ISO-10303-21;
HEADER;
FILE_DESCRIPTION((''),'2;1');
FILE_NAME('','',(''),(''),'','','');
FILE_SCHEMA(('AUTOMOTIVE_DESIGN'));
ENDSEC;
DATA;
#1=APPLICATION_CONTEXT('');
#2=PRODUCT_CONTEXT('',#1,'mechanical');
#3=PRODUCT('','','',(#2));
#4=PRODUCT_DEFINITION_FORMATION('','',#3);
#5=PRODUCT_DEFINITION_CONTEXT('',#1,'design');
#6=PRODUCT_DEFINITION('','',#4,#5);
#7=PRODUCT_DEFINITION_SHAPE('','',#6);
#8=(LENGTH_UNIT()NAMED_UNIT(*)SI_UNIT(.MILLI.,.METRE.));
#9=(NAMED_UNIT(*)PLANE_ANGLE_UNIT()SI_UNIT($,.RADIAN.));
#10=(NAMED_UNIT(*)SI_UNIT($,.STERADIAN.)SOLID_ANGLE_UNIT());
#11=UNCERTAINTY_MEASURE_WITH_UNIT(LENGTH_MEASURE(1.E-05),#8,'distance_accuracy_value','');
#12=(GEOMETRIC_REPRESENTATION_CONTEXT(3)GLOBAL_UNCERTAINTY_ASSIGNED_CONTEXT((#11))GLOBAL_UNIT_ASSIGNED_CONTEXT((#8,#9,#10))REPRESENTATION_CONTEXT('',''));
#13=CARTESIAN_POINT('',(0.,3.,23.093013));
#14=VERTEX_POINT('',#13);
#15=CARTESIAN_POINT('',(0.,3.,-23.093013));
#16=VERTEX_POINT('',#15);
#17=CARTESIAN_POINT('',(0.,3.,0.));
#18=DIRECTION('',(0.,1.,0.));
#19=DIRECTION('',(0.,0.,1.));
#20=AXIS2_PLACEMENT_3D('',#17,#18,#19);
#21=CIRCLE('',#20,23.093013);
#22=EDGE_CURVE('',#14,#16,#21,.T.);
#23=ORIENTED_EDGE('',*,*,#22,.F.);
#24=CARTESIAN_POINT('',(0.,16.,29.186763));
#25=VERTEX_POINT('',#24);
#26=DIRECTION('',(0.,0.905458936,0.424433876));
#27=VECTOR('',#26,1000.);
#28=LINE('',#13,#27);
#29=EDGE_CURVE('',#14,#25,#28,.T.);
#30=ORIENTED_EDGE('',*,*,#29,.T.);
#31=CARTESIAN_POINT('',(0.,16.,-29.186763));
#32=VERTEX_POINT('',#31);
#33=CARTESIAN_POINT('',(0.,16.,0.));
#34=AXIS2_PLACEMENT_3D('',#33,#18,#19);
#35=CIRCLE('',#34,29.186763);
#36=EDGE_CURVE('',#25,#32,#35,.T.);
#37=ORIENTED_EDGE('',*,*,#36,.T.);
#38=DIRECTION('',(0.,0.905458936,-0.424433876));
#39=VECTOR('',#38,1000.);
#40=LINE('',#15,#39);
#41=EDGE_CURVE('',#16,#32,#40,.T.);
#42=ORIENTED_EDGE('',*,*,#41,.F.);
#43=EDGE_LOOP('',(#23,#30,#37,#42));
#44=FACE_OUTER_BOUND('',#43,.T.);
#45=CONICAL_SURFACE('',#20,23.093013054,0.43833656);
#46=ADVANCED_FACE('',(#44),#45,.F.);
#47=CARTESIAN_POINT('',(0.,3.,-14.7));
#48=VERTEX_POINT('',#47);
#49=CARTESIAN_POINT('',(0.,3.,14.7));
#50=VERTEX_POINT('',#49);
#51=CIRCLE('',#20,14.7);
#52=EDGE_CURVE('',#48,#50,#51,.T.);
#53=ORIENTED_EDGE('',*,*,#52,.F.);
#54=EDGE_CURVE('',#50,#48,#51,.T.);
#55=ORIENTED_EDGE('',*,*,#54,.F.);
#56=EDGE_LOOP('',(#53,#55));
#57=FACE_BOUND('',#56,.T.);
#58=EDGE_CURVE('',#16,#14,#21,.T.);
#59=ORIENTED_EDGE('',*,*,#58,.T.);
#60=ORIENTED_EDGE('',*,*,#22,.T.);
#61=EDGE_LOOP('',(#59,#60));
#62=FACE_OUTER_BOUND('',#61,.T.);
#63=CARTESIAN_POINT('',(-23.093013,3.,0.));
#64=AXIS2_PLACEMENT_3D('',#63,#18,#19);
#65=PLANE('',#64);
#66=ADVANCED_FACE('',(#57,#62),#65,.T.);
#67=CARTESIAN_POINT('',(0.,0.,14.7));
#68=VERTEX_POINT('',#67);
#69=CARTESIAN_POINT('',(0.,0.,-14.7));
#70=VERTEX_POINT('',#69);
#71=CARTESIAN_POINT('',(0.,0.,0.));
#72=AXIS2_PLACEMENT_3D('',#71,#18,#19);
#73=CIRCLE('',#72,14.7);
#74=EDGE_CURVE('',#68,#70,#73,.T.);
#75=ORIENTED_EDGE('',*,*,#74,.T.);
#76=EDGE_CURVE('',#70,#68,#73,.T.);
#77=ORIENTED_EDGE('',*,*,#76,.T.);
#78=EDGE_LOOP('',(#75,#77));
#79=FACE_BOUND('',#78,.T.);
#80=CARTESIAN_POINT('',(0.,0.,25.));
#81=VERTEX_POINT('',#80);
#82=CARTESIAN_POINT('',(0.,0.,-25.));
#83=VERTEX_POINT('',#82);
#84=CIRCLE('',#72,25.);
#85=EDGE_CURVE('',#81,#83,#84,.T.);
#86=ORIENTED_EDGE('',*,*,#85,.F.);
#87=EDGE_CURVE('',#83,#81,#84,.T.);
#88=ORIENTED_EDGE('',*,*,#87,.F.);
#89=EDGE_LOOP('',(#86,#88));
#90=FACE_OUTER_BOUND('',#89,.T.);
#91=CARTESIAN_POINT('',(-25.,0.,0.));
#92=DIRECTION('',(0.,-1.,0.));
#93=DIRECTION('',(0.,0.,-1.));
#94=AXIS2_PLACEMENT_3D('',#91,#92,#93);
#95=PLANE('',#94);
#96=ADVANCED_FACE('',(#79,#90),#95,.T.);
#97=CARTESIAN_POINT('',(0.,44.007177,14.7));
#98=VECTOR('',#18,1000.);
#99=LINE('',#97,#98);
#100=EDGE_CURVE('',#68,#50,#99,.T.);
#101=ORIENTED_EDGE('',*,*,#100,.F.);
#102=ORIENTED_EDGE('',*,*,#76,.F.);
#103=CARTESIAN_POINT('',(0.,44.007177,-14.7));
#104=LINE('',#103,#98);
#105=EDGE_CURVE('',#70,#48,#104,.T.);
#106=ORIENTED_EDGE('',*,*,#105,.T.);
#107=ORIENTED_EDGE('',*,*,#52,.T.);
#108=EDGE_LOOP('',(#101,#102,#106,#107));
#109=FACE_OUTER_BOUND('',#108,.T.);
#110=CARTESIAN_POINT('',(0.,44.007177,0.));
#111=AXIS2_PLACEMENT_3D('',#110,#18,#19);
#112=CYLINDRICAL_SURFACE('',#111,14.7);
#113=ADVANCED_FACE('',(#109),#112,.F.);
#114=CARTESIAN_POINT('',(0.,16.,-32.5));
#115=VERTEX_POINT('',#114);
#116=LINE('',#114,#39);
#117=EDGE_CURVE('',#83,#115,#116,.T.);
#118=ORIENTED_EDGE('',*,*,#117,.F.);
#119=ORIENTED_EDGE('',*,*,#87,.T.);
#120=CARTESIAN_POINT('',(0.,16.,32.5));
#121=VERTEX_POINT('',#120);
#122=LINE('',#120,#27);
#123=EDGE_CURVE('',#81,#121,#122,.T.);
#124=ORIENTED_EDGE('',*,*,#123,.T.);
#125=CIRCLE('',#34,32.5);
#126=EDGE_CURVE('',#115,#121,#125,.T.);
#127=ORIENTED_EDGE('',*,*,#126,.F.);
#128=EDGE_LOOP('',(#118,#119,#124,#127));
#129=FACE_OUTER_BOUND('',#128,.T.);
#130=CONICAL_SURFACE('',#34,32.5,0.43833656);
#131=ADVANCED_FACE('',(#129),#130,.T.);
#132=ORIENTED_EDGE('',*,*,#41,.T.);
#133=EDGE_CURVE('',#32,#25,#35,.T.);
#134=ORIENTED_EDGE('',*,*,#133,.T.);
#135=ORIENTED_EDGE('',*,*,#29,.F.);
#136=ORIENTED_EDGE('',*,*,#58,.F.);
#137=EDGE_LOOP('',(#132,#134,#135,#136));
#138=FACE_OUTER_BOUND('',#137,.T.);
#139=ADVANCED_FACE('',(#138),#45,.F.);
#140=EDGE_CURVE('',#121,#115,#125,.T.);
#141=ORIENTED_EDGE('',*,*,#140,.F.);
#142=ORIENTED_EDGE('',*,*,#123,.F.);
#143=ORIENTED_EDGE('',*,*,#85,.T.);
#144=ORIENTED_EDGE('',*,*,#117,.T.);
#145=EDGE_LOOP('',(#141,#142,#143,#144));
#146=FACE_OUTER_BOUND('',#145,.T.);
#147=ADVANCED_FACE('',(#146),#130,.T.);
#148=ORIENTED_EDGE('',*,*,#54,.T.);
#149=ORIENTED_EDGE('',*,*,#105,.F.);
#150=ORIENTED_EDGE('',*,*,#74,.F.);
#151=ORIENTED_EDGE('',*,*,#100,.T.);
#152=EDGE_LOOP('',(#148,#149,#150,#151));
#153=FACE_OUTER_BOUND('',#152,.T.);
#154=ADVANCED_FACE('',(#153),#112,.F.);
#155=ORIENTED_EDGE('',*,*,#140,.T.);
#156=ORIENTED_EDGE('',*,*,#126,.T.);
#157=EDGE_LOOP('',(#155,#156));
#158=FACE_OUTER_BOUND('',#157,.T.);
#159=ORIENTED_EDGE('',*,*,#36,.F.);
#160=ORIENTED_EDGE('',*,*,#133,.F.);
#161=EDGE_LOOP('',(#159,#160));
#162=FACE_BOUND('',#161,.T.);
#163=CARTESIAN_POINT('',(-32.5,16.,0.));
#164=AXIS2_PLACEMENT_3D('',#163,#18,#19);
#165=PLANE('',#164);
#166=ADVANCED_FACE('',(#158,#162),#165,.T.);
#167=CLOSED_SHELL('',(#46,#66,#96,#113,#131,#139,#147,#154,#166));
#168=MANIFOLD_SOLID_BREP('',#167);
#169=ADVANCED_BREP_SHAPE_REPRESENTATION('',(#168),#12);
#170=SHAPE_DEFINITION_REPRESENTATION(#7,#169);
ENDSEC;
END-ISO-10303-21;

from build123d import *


with BuildPart() as part:
    # 草图1 → 旋转1 (revolve)
    with BuildSketch(Plane.XY, mode=Mode.PRIVATE) as revolve_1_sk:
        Polygon((-32.5, 16), (-25, 0), (-14.7, 0), (-14.7, 3), (-23.093013054, 3), (-29.186763054, 16), align=None)
    revolve(revolve_1_sk.sketch.rotate(Axis((0, 44.007177033, 0), (0, -1, 0)), 270), axis=Axis((0, 44.007177033, 0), (0, -1, 0)))


solid = part.part
